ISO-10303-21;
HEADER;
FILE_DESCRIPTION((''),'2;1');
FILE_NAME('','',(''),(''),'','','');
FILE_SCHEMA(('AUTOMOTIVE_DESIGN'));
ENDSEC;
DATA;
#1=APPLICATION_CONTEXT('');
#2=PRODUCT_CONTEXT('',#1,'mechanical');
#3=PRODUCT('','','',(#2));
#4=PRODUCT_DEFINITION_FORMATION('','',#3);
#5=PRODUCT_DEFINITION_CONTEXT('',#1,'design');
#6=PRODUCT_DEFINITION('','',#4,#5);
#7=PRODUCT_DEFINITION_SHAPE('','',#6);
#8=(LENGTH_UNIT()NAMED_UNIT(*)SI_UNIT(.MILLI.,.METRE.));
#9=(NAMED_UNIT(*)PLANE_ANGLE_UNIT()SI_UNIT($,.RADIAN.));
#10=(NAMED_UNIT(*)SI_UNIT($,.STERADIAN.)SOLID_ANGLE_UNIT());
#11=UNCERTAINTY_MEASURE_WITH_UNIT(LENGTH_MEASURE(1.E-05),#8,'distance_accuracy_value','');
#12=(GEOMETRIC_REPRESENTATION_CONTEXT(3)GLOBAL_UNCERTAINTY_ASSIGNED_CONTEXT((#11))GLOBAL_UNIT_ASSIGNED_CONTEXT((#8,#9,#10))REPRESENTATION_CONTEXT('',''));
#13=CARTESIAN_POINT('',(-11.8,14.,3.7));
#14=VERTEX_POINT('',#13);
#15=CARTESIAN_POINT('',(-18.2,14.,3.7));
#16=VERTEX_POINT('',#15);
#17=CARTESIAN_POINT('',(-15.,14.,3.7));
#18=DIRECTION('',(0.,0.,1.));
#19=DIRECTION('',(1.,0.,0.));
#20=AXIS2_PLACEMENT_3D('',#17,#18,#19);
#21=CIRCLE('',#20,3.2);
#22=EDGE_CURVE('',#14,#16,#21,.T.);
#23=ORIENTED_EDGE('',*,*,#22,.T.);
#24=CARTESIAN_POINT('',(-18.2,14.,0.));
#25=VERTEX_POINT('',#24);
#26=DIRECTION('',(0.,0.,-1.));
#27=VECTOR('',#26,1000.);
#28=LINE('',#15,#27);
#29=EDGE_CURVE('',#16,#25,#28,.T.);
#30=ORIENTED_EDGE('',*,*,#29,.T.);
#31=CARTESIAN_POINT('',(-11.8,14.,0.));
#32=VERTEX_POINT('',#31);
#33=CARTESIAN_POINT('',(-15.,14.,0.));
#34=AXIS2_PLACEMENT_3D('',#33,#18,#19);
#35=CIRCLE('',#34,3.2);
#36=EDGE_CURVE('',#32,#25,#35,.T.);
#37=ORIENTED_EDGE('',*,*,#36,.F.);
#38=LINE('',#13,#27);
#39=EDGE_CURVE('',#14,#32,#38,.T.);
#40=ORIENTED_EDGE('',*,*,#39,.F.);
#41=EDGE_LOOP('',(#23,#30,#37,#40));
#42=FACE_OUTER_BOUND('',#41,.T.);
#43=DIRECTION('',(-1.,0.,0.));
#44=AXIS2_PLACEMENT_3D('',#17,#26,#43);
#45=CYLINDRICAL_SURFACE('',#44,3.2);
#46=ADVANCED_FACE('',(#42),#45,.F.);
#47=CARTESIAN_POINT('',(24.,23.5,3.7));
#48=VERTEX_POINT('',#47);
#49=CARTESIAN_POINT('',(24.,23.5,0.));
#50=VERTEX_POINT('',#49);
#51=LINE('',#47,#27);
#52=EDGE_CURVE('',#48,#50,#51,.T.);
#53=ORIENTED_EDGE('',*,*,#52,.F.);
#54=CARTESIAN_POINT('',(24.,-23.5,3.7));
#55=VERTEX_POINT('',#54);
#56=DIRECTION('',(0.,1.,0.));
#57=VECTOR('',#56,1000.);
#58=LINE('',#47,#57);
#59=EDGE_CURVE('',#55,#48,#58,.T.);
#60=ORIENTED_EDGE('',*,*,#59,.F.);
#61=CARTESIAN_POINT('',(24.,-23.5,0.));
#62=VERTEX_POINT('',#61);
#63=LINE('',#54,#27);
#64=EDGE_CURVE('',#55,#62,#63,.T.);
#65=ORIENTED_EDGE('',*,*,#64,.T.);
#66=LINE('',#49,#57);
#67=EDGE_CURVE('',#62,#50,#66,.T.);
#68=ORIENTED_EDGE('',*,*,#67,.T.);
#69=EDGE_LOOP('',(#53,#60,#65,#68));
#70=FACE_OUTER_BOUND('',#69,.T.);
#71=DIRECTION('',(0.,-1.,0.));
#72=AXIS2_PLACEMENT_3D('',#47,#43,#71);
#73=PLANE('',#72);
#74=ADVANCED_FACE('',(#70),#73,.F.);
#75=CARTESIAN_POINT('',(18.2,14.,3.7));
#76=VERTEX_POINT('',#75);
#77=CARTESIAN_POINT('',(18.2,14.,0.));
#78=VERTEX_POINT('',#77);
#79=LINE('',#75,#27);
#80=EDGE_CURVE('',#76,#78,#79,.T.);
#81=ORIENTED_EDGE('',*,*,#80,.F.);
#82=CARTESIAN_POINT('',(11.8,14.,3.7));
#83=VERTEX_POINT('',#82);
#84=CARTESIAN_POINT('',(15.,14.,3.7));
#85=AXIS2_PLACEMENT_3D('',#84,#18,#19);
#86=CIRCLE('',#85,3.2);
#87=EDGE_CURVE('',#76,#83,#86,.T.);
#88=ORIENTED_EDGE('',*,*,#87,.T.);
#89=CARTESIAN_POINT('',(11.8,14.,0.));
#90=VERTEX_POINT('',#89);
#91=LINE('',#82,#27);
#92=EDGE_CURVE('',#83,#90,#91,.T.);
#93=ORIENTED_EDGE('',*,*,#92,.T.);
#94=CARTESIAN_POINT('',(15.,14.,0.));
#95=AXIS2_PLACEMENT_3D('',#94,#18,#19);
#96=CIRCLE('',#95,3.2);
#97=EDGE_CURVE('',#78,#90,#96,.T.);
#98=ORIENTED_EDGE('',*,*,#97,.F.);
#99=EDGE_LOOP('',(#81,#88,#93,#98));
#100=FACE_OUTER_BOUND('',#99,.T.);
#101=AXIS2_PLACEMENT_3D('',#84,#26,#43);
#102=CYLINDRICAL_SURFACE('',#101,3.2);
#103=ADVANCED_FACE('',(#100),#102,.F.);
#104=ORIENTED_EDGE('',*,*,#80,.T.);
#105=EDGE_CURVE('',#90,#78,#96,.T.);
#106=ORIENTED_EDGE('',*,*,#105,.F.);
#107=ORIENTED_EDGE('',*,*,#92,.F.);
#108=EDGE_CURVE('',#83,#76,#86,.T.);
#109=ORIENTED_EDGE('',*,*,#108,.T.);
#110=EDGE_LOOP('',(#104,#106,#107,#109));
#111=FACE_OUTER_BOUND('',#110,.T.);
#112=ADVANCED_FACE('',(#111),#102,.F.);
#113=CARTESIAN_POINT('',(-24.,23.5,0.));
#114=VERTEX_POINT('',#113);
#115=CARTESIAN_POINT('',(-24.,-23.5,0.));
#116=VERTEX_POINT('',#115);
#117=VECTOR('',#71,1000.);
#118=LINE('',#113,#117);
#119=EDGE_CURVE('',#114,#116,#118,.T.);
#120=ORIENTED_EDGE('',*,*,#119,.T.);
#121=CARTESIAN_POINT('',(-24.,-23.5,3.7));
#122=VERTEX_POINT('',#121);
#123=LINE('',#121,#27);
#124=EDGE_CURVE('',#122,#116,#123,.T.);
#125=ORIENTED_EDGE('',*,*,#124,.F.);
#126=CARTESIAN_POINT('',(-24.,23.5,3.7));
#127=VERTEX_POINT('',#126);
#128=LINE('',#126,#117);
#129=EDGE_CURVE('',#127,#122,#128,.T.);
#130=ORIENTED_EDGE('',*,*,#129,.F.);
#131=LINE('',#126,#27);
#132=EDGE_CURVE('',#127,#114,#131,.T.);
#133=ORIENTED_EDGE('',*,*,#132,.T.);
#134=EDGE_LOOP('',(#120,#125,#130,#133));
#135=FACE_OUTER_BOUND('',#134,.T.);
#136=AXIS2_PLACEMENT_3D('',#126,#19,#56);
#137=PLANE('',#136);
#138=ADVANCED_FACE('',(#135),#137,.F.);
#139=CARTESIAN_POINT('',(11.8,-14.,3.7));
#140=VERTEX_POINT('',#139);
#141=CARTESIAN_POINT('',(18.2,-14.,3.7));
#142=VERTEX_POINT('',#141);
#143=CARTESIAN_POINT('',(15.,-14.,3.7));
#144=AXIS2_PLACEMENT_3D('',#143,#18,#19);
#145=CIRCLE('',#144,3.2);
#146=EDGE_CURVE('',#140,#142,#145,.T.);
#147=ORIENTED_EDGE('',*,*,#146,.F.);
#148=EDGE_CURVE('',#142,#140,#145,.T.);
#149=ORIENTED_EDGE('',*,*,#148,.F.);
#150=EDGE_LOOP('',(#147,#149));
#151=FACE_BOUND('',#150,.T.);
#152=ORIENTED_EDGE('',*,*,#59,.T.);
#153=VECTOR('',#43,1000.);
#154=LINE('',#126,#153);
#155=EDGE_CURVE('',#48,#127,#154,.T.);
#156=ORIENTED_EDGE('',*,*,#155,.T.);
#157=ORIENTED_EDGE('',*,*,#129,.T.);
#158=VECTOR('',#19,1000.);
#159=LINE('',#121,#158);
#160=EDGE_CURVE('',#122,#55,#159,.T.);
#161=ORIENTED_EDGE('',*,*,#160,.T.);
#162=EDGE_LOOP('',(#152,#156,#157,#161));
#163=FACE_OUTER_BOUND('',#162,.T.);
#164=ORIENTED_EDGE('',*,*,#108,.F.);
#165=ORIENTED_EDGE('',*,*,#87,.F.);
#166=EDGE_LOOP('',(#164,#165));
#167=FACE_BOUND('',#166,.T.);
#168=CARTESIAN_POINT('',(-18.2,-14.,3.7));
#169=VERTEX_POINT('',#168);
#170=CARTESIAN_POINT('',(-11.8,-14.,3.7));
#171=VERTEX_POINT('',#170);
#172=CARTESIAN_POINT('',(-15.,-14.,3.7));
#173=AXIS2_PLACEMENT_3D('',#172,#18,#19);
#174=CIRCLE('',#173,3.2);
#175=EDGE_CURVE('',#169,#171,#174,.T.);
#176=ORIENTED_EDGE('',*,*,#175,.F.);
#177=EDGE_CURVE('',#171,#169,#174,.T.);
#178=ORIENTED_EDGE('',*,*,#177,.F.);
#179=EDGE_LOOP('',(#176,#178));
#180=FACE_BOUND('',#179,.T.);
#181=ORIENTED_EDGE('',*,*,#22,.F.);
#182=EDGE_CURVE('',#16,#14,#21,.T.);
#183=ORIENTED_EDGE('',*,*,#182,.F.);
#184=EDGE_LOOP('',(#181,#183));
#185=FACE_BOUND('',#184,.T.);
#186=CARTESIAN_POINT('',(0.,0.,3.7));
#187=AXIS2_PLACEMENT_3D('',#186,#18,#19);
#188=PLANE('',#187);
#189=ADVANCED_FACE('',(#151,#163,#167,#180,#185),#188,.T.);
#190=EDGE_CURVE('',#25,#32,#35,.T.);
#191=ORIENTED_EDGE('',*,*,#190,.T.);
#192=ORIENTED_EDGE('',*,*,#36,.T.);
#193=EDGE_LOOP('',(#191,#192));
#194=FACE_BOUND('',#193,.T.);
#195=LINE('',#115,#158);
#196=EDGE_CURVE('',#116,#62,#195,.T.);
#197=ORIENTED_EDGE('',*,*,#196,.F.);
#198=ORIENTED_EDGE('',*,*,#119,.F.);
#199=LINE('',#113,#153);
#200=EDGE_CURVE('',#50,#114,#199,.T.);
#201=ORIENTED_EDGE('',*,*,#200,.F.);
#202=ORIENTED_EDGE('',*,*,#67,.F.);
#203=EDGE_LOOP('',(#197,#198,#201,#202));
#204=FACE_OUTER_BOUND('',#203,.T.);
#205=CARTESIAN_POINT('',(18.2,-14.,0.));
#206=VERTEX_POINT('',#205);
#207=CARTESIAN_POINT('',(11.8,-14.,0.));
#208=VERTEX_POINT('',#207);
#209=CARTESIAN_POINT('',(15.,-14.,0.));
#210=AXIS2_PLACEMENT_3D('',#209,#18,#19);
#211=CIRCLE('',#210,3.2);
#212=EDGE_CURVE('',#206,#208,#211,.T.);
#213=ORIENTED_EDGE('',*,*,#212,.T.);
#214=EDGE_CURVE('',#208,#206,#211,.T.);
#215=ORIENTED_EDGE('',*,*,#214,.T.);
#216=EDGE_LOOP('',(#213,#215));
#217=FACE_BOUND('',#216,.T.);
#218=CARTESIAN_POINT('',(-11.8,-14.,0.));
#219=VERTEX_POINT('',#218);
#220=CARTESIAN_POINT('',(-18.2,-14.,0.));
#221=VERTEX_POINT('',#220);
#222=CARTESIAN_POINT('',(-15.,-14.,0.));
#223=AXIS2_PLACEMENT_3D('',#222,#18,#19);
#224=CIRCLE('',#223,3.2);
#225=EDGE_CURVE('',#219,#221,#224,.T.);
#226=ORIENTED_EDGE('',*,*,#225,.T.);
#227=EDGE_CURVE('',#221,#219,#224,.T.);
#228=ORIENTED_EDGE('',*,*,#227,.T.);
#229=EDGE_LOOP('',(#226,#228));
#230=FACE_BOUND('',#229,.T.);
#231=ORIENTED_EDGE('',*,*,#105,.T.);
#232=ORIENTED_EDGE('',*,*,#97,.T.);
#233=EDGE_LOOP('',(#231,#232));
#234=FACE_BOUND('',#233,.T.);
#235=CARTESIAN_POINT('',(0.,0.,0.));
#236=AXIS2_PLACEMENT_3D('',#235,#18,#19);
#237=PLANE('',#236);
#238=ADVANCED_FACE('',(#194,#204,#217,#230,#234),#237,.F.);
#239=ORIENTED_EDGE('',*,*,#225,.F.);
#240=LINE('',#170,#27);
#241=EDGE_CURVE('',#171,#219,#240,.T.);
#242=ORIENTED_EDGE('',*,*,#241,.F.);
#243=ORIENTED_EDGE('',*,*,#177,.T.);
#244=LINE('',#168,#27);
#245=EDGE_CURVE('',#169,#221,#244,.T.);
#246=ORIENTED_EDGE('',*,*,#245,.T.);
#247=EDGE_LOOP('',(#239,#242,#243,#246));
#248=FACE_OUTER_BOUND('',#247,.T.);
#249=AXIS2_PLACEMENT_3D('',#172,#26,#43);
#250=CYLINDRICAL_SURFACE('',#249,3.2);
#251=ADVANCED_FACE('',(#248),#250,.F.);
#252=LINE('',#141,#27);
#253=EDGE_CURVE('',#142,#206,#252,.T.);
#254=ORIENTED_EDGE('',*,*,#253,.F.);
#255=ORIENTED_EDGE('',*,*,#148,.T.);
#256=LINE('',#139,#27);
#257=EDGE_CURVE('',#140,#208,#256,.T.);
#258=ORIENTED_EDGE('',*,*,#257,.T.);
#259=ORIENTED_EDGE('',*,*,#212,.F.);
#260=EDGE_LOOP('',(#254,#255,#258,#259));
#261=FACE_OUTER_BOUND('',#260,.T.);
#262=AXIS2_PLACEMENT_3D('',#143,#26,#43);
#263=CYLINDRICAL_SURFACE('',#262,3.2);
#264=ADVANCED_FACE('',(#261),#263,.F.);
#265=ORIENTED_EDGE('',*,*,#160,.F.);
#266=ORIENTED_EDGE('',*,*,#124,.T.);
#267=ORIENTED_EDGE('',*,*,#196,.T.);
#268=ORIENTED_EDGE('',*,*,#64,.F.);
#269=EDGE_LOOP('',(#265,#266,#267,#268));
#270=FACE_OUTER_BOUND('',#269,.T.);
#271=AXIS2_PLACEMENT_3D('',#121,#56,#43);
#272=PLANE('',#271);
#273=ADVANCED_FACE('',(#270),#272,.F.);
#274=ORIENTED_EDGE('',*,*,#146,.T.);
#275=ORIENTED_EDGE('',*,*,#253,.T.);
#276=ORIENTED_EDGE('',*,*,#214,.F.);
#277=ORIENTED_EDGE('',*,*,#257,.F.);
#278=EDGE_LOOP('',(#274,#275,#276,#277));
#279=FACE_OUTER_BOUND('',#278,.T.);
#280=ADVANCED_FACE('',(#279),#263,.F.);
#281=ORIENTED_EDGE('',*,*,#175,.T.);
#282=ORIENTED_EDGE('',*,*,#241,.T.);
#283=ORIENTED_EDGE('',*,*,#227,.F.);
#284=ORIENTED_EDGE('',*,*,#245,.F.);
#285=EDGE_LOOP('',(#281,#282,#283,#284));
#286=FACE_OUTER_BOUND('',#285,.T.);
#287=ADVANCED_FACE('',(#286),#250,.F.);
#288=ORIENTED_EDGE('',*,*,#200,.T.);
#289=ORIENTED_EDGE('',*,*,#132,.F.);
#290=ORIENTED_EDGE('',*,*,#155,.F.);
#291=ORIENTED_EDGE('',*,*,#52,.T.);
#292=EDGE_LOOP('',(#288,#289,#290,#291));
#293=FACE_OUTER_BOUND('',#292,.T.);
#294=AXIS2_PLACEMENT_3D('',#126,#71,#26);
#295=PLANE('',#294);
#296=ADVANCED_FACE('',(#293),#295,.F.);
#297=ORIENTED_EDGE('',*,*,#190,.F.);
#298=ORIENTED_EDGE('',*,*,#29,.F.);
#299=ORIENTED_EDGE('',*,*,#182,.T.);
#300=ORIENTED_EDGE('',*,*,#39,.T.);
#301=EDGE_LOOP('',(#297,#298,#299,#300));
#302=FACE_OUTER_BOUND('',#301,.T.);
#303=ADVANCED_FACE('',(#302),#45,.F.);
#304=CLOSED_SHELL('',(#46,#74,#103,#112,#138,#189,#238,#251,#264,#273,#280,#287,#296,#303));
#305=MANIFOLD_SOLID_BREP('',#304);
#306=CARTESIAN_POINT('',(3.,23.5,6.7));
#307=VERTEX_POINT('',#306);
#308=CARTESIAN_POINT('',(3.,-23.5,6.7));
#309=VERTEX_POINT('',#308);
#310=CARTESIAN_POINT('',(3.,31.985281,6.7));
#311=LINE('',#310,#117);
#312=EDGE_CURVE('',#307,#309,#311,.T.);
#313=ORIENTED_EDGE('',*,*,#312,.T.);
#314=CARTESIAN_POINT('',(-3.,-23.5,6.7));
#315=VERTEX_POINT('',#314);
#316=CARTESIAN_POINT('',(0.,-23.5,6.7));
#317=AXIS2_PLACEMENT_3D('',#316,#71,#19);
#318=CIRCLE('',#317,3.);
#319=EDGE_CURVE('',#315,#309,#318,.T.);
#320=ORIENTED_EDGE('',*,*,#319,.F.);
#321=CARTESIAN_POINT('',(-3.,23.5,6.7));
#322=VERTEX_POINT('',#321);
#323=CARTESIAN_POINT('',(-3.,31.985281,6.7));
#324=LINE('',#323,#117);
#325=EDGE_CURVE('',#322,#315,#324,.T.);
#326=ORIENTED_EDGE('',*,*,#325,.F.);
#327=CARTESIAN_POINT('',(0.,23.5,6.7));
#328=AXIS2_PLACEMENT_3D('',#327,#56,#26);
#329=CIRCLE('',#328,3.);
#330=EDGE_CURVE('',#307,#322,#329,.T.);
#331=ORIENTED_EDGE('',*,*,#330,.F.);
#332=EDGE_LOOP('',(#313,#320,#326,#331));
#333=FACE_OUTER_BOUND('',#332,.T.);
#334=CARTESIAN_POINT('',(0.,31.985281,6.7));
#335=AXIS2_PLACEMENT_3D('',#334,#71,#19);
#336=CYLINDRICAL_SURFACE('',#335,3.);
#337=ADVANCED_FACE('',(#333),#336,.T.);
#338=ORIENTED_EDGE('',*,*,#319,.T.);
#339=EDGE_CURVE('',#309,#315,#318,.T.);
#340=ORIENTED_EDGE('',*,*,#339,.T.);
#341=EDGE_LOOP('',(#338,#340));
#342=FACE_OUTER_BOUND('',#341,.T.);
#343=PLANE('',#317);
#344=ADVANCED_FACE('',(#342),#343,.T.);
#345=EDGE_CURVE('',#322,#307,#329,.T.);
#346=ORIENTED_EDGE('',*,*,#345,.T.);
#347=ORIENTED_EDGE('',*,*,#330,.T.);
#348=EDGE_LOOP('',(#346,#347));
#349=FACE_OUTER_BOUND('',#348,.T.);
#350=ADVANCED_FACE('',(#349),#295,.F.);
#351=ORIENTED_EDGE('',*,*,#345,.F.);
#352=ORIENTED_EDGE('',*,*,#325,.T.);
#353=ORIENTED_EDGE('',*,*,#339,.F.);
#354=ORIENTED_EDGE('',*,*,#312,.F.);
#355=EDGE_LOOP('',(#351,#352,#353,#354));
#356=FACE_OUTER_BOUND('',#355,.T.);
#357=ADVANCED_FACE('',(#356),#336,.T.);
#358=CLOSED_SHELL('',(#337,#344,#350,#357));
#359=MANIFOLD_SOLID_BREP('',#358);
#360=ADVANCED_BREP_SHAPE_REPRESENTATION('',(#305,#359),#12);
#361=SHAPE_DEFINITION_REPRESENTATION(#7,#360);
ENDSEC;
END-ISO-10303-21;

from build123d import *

# Parameters (mm, degrees)
SKETCH_1_W      = 48
SKETCH_1_H      = 47
SKETCH_1_R      = 3.2
EXTRUDE_1_DEPTH = 3.7
SKETCH_2_R      = 3
EXTRUDE_2_DEPTH = 47


with BuildPart() as part:
    # 草图1 → 凸台-拉伸1 (new body)
    with BuildSketch(Plane.XY):
        Rectangle(SKETCH_1_W, SKETCH_1_H)
        with Locations((-15, 14)):
            Circle(SKETCH_1_R, mode=Mode.SUBTRACT)
        with Locations((-15, -14)):
            Circle(SKETCH_1_R, mode=Mode.SUBTRACT)
        with Locations((15, 14)):
            Circle(SKETCH_1_R, mode=Mode.SUBTRACT)
        with Locations((15, -14)):
            Circle(SKETCH_1_R, mode=Mode.SUBTRACT)
    extrude(amount=EXTRUDE_1_DEPTH)


with BuildPart() as body_2:
    # 草图2 → 凸台-拉伸2 (new body)
    with BuildSketch(Plane.XZ.offset(23.5)):
        with Locations((0, 6.7)):
            Circle(SKETCH_2_R)
    extrude(amount=-EXTRUDE_2_DEPTH)


solid = Compound([part.part, body_2.part])
